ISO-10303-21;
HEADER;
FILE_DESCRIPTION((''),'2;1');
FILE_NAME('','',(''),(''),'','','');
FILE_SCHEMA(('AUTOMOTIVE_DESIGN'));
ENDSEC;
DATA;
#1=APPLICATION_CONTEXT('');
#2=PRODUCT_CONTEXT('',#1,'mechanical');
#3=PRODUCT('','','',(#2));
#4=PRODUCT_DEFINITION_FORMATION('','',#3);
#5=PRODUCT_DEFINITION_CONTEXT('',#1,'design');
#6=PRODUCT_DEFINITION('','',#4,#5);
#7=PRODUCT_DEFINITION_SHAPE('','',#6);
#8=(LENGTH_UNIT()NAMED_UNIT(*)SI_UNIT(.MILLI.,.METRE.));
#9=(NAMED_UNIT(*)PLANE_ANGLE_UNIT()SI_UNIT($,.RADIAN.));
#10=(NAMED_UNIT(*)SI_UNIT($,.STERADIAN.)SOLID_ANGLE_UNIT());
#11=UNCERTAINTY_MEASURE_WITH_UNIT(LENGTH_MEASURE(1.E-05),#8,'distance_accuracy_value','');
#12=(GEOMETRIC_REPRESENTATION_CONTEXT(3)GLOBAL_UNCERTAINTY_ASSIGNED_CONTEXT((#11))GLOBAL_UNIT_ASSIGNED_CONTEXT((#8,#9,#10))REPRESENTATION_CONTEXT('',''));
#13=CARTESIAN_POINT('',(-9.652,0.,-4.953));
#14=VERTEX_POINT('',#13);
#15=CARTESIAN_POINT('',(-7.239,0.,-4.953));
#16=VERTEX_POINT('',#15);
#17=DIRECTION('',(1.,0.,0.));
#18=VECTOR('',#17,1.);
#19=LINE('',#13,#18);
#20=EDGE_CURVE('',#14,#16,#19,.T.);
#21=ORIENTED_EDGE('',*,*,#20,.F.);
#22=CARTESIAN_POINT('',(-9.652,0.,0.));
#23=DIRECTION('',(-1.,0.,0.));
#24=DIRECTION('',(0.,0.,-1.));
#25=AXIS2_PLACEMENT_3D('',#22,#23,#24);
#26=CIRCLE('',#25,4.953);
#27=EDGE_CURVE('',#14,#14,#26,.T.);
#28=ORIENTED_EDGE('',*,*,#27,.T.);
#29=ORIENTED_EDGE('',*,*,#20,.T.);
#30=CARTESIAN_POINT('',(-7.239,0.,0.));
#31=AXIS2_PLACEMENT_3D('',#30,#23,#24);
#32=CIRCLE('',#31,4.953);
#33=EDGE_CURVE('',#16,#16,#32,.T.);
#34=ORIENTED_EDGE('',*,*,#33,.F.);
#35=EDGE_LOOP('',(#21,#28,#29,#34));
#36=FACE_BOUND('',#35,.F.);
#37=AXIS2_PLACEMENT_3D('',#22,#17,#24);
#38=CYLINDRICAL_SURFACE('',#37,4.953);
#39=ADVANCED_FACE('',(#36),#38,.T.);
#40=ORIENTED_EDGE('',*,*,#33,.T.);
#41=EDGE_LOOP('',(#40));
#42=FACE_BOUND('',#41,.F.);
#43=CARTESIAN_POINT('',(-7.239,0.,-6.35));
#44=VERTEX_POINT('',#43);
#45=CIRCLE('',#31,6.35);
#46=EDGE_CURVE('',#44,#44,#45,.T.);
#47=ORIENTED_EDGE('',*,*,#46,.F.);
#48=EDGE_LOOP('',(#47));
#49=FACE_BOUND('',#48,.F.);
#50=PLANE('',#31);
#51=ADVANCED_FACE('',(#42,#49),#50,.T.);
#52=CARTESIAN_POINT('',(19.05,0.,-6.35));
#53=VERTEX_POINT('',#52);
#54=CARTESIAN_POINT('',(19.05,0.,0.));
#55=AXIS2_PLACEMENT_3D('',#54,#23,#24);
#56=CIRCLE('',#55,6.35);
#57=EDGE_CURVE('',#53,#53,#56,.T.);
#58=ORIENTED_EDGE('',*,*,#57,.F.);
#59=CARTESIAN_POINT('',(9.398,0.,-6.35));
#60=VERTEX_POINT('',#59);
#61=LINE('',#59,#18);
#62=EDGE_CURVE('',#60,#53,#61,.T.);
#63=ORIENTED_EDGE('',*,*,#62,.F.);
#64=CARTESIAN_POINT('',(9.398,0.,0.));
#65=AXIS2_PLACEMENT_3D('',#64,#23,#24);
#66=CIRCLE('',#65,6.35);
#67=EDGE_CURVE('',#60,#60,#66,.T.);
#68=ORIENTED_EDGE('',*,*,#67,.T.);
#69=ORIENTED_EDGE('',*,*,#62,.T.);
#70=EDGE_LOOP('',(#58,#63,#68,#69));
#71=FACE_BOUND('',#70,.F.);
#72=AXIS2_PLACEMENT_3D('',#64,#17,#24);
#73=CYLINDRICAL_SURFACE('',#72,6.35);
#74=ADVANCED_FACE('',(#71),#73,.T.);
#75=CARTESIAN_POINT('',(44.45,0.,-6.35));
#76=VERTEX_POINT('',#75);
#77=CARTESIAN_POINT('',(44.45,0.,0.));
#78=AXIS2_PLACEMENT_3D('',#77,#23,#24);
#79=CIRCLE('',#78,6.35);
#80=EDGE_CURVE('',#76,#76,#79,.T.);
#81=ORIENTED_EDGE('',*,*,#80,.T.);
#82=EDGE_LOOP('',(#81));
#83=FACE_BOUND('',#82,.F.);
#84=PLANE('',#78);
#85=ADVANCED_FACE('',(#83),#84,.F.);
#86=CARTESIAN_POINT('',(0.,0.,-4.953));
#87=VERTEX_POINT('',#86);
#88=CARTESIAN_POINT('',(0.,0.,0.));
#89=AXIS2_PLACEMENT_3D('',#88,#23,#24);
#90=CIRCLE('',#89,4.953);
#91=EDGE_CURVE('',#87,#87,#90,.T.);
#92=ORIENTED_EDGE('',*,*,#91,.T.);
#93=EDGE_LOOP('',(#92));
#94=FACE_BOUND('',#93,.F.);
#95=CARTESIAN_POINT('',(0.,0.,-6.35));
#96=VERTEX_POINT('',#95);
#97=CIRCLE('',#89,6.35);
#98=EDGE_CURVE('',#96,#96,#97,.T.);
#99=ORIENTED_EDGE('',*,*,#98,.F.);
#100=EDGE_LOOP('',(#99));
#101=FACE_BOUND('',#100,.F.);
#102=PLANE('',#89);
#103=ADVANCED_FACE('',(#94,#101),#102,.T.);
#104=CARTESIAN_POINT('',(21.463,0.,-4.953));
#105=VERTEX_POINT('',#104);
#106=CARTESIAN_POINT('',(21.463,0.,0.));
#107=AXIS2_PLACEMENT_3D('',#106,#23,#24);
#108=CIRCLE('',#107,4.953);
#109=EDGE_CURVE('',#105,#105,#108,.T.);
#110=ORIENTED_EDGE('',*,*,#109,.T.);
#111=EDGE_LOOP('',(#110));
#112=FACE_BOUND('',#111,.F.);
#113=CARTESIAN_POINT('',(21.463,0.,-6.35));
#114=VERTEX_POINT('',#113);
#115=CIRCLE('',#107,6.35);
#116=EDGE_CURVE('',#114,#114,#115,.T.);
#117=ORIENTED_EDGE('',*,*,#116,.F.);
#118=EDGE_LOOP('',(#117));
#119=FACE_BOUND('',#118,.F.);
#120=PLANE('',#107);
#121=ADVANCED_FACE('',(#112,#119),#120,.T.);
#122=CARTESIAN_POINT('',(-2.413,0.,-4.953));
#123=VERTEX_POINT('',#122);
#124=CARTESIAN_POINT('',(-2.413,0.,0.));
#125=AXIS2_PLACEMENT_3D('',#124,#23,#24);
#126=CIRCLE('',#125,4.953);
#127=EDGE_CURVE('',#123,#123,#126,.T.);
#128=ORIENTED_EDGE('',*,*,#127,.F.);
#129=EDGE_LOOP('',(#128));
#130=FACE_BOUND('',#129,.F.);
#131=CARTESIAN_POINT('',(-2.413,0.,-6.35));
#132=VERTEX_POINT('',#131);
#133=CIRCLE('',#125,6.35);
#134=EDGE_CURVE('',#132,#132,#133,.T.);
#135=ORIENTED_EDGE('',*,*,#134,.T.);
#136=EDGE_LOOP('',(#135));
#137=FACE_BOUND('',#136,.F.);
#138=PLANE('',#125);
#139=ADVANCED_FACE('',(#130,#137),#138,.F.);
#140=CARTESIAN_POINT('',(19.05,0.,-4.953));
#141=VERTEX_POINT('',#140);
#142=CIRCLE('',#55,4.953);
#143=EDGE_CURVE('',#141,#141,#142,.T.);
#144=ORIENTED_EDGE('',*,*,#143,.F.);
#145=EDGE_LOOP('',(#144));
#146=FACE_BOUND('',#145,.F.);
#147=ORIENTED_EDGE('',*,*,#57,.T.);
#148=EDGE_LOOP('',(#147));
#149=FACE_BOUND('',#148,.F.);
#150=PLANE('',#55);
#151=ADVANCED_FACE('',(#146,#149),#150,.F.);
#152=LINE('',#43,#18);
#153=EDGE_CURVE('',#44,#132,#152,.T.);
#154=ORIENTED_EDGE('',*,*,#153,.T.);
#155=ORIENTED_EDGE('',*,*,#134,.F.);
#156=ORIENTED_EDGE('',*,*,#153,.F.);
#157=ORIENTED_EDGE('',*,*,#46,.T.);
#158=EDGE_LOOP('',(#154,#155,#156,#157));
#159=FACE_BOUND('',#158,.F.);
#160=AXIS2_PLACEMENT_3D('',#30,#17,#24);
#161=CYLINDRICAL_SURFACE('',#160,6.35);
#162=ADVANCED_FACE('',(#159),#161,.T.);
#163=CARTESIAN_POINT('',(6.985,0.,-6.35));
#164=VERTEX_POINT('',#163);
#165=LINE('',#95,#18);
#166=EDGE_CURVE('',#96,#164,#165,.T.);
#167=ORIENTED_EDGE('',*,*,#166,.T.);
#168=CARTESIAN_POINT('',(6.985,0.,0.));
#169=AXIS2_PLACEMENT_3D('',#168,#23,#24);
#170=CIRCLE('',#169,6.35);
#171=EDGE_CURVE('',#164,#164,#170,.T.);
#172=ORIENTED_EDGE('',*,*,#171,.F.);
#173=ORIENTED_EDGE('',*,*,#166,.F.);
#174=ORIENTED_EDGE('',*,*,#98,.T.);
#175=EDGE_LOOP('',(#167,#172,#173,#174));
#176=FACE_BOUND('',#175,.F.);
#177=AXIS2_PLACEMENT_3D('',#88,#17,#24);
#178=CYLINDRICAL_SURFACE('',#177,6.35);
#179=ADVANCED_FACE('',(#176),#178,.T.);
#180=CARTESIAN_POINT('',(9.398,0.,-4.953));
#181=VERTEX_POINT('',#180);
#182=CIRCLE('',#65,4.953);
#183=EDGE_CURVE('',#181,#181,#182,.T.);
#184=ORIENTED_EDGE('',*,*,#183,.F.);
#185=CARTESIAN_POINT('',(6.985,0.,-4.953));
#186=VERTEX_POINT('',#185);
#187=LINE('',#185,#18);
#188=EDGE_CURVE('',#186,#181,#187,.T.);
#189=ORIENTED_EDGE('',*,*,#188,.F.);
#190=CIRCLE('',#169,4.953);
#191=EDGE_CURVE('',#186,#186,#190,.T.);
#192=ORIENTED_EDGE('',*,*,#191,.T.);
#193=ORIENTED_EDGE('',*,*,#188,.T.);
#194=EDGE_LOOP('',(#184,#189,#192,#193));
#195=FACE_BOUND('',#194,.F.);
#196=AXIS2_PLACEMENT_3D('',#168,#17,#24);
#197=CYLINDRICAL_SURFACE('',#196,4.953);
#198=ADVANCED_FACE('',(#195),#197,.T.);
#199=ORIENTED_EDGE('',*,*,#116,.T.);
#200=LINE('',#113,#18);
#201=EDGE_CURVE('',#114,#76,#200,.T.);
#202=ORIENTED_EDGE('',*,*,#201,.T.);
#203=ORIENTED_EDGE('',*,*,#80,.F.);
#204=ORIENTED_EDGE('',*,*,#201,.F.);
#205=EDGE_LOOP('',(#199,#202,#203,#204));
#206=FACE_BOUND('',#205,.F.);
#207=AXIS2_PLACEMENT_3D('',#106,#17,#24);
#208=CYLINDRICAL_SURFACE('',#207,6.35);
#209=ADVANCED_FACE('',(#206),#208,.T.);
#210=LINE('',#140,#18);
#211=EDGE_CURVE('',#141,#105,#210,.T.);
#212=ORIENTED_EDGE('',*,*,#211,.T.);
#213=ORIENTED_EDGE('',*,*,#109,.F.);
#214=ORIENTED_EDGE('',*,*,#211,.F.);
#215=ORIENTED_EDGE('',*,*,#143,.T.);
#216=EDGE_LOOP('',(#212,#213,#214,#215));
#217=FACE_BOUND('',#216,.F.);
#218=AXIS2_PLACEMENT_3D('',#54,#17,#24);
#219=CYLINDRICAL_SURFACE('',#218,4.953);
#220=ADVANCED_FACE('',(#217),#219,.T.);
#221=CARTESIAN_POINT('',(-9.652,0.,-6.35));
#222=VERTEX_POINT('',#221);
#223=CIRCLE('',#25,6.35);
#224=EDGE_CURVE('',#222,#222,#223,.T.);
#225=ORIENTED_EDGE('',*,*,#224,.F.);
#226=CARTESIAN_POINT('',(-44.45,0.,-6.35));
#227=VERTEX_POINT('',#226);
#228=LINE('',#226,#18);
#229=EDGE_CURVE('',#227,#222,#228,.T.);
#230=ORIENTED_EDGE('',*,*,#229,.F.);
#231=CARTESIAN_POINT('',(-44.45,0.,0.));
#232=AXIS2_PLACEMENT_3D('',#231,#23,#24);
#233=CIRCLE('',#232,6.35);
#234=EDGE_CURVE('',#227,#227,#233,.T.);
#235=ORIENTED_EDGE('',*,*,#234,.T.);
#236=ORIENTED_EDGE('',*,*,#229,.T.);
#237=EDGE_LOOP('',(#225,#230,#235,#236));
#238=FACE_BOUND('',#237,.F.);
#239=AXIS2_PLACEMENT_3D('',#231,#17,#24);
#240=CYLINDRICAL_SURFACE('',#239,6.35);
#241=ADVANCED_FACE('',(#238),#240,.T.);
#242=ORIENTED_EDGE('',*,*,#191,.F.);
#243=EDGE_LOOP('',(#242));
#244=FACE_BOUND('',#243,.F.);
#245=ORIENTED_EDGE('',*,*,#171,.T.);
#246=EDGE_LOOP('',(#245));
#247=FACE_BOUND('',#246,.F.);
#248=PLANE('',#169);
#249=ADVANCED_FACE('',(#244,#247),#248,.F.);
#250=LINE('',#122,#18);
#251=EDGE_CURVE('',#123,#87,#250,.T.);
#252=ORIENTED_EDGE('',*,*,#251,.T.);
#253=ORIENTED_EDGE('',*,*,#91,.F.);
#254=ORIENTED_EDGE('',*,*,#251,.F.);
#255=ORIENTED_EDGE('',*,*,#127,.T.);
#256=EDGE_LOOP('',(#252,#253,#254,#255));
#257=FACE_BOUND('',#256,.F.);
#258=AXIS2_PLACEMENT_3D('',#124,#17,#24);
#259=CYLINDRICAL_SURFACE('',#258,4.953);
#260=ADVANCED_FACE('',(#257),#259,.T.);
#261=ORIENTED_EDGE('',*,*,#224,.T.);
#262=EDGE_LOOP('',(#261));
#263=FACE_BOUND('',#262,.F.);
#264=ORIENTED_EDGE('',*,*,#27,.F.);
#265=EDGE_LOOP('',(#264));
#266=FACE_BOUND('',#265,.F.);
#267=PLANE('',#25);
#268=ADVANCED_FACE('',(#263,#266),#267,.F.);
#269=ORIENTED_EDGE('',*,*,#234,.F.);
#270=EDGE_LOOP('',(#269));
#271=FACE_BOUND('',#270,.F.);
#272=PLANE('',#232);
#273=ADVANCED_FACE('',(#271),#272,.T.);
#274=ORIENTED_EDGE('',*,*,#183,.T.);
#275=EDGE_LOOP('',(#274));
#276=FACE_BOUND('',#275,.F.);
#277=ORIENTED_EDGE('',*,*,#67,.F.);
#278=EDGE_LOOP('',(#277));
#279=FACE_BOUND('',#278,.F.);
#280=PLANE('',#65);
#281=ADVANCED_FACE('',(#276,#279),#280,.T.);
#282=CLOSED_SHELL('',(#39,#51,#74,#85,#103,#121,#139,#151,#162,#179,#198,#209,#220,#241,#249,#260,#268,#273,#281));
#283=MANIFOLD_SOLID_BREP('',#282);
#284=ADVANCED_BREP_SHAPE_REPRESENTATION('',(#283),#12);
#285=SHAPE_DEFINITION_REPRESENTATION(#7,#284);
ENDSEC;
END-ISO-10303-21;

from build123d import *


with BuildPart() as part:
    # Rod Half-Profile Sketch → Grooved Rod Revolve (revolve)
    with BuildSketch(Plane.XY, mode=Mode.PRIVATE) as grooved_rod_revolve_sk:
        Polygon((-44.45, 0), (-44.45, 6.35), (-9.652, 6.35), (-9.652, 4.953), (-7.239, 4.953), (-7.239, 6.35), (-2.413, 6.35), (-2.413, 4.953), (0, 4.953), (0, 6.35), (6.985, 6.35), (6.985, 4.953), (9.398, 4.953), (9.398, 6.35), (19.05, 6.35), (19.05, 4.953), (21.463, 4.953), (21.463, 6.35), (44.45, 6.35), (44.45, 0), align=None)
    revolve(grooved_rod_revolve_sk.sketch.rotate(Axis((49.991353887, 0, 0), (-1, 0, 0)), 90), axis=Axis((49.991353887, 0, 0), (-1, 0, 0)))


solid = part.part
